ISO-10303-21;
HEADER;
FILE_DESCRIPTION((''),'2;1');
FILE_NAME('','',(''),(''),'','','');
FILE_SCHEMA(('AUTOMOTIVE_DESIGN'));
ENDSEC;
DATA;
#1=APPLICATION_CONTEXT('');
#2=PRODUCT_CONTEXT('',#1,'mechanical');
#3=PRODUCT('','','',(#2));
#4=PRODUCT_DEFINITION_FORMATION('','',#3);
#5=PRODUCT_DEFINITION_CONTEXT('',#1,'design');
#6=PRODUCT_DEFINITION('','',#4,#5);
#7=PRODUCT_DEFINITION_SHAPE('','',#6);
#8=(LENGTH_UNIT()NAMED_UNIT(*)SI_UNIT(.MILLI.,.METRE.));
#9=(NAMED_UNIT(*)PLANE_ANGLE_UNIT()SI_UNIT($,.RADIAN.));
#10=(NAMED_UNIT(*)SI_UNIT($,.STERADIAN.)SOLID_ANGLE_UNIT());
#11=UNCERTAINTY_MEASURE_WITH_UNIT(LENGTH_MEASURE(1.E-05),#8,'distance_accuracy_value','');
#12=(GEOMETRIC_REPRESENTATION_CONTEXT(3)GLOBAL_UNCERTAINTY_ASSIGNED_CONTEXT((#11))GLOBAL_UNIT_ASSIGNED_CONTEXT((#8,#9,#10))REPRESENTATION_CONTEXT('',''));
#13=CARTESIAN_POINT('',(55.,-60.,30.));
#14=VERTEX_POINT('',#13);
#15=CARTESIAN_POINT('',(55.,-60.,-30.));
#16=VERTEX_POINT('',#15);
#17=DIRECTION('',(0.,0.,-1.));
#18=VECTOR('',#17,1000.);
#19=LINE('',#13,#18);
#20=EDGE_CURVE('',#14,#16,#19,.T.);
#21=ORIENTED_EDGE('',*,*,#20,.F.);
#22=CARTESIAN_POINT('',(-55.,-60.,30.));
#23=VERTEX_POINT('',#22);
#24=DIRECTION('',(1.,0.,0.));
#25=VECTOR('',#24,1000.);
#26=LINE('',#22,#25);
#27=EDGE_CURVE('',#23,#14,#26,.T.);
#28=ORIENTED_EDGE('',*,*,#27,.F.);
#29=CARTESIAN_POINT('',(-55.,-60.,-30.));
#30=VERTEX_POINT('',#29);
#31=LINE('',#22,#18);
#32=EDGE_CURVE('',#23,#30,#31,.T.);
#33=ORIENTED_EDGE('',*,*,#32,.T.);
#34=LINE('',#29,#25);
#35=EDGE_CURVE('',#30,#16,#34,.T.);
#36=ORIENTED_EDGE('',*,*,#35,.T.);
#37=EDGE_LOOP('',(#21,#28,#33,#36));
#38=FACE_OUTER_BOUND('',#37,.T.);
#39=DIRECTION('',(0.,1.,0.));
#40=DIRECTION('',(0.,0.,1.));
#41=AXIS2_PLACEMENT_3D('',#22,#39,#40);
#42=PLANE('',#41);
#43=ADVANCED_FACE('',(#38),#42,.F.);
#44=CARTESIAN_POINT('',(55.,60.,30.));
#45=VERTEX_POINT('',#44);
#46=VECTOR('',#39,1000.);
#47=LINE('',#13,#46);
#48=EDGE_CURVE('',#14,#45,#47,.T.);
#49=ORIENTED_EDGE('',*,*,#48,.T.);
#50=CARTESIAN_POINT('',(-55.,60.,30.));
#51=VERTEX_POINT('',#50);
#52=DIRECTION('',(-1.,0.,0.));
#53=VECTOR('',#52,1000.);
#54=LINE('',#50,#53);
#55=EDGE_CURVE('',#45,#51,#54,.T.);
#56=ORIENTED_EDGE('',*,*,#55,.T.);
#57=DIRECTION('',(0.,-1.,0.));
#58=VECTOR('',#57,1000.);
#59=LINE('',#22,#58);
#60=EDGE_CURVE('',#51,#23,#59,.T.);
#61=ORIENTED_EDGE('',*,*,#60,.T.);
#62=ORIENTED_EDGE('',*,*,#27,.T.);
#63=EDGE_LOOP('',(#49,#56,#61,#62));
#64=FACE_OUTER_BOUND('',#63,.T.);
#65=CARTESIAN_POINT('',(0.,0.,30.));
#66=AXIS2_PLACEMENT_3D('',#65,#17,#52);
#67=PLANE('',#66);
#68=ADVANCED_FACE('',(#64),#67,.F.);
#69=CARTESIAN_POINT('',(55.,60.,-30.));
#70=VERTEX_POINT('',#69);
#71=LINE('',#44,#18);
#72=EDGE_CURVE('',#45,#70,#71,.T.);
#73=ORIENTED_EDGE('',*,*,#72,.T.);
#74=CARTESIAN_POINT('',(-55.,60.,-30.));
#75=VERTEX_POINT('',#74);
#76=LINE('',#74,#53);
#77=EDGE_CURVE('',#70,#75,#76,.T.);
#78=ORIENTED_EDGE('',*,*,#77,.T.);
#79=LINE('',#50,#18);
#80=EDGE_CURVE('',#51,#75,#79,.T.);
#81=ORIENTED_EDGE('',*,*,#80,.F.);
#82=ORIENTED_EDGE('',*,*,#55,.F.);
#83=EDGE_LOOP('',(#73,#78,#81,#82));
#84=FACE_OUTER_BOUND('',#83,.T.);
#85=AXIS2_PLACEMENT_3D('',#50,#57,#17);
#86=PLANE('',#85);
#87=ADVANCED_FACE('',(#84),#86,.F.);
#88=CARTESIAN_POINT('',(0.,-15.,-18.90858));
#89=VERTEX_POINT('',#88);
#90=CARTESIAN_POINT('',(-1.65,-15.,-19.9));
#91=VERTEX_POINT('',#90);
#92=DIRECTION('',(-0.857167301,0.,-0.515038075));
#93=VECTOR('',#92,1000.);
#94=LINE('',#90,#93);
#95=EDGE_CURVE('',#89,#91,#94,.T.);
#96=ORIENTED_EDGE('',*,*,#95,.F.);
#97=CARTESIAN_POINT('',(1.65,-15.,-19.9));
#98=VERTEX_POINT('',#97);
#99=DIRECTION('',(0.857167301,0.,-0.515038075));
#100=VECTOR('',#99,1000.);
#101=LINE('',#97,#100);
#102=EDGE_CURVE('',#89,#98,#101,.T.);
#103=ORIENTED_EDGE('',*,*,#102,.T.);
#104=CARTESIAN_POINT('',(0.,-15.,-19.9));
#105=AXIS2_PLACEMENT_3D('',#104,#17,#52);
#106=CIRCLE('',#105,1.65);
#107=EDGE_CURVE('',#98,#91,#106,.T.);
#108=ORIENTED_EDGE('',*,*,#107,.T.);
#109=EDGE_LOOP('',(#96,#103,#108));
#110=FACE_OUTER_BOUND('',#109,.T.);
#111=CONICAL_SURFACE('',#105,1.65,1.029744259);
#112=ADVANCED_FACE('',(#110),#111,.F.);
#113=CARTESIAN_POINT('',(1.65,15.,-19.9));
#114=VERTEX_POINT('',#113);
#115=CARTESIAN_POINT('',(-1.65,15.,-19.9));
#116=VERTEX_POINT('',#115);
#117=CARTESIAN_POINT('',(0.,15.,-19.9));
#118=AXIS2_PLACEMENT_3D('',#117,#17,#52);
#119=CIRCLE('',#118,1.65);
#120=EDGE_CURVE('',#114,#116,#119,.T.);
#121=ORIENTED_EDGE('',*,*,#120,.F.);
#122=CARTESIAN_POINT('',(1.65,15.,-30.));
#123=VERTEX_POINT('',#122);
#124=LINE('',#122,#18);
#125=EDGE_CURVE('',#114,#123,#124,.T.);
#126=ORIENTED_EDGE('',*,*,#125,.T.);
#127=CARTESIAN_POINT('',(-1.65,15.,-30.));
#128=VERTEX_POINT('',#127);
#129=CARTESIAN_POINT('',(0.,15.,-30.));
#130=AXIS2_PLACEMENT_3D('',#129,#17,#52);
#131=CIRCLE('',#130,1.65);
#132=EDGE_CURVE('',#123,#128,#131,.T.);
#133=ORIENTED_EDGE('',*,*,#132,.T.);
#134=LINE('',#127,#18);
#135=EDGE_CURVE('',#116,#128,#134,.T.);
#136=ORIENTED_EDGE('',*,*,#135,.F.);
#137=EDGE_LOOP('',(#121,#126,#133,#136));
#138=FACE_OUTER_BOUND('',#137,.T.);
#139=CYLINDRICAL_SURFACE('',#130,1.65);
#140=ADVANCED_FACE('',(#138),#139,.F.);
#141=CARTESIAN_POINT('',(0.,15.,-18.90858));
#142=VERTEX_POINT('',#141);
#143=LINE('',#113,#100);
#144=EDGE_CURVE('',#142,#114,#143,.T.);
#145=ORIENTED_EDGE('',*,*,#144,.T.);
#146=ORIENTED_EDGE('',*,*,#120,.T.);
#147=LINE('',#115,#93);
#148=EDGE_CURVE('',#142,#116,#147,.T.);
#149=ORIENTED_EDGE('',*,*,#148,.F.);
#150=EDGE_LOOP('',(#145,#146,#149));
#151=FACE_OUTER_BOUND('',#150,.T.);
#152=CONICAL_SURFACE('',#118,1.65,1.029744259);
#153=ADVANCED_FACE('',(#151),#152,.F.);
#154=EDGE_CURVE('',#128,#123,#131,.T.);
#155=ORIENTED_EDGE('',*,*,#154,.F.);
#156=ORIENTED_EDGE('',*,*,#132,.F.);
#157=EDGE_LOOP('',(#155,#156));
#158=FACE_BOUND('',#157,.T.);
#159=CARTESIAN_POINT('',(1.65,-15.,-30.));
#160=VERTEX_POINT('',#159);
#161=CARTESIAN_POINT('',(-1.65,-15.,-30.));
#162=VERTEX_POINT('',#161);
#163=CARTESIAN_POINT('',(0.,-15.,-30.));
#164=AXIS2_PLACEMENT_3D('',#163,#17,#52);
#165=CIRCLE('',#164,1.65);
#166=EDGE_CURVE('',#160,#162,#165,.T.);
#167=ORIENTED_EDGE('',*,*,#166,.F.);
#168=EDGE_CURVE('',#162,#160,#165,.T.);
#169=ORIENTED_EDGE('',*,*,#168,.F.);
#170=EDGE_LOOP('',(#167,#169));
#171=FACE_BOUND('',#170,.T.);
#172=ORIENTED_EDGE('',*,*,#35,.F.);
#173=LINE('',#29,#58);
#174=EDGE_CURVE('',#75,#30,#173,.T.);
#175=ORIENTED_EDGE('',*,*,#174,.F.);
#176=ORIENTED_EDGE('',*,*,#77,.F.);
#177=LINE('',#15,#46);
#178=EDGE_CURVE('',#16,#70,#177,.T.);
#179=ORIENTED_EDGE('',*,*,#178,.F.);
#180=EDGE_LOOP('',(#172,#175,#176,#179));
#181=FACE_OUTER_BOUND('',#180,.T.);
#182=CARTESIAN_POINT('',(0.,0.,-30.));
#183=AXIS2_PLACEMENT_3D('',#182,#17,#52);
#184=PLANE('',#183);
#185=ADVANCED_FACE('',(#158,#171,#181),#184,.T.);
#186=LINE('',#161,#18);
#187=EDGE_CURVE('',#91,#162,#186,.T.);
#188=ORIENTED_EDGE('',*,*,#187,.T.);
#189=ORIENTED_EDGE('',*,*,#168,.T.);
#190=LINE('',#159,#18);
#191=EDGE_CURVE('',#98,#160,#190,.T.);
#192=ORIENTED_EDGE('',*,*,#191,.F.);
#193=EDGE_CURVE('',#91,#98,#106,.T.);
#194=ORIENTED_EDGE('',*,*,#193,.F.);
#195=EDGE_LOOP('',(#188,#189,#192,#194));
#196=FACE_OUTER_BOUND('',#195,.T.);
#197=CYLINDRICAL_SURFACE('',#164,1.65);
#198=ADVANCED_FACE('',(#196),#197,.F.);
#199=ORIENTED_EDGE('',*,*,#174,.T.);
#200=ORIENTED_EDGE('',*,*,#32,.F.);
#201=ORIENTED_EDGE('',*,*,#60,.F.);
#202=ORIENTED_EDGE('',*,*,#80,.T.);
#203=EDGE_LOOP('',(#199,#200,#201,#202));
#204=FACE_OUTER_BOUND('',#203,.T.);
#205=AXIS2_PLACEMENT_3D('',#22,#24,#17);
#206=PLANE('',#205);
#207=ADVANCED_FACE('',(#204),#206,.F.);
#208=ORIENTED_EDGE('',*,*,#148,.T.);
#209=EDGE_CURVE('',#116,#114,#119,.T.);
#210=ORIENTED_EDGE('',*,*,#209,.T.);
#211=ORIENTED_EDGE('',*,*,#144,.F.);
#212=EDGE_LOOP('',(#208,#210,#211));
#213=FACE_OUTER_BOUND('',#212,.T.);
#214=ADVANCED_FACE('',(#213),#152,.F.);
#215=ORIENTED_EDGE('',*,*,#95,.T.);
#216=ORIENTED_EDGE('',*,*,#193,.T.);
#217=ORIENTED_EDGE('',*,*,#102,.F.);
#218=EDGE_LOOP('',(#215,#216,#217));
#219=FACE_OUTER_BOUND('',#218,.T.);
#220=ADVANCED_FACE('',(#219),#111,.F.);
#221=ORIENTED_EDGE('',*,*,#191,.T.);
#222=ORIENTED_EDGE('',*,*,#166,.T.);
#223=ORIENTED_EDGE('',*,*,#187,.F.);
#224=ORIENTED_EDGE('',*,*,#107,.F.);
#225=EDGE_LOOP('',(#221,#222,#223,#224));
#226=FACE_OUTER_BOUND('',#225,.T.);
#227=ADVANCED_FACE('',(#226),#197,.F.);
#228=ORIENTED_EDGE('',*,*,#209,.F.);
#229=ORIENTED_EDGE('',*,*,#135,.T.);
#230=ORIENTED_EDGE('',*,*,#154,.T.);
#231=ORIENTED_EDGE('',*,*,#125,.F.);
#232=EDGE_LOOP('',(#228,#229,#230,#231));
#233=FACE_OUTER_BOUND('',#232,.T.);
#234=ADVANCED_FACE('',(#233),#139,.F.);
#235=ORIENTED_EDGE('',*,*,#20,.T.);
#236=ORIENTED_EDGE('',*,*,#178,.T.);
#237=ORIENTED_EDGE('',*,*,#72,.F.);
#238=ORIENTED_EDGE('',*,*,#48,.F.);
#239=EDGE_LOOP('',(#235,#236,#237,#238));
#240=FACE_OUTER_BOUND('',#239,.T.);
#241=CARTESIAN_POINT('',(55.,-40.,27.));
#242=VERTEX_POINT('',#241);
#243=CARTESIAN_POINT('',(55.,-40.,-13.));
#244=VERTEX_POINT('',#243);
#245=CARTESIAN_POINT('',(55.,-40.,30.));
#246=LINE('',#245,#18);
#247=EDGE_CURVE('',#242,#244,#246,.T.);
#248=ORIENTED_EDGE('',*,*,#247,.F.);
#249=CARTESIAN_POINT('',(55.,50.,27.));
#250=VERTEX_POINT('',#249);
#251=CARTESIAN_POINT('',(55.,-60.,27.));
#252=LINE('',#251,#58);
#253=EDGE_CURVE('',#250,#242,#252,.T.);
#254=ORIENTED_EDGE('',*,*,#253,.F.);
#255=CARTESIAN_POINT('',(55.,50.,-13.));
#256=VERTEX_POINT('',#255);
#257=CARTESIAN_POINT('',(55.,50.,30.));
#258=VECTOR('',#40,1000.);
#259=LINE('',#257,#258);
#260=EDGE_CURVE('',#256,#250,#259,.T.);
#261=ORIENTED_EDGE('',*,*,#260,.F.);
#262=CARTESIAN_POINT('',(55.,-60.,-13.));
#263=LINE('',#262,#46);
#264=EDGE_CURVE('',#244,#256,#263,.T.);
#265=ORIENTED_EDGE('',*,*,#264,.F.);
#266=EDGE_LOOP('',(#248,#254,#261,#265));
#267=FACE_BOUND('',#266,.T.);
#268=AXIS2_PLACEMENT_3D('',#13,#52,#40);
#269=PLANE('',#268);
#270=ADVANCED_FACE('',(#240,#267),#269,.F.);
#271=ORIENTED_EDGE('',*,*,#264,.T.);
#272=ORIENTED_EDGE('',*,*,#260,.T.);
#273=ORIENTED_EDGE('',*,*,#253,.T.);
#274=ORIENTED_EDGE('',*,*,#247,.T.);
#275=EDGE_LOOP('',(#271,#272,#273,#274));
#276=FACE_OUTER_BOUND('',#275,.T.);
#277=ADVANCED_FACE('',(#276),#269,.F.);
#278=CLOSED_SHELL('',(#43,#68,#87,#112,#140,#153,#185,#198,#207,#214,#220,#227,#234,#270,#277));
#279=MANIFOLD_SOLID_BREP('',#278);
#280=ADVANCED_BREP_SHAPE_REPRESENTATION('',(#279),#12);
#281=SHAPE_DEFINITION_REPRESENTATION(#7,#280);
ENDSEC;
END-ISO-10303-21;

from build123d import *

# Parameters (mm, degrees)
SKETCH_1_W             = 110
SKETCH_1_H             = 120
EXTRUDE_1_DEPTH        = 30
HOLE_WIZARD_M4_1_D     = 3.3
HOLE_WIZARD_M4_1_DEPTH = 10.1
HOLE_WIZARD_M4_1_TIP   = 0.991420021


with BuildPart() as part:
    # 草图1 → 凸台-拉伸1 (new, symmetric)
    with BuildSketch(Plane.XY):
        Rectangle(SKETCH_1_W, SKETCH_1_H)
    extrude(amount=EXTRUDE_1_DEPTH, both=True)

    # M4 螺纹孔1
    with Locations(Plane(origin=(0, 0, -30), x_dir=(-1, 0, 0), z_dir=(0, 0, -1))):
        with Locations((0, 15), (0, -15)):
            Hole(HOLE_WIZARD_M4_1_D / 2, depth=HOLE_WIZARD_M4_1_DEPTH)
            with Locations((0, 0, -(HOLE_WIZARD_M4_1_DEPTH + HOLE_WIZARD_M4_1_TIP / 2))):  # 118° drill point
                Cone(0, HOLE_WIZARD_M4_1_D / 2, HOLE_WIZARD_M4_1_TIP, mode=Mode.SUBTRACT)


solid = part.part
